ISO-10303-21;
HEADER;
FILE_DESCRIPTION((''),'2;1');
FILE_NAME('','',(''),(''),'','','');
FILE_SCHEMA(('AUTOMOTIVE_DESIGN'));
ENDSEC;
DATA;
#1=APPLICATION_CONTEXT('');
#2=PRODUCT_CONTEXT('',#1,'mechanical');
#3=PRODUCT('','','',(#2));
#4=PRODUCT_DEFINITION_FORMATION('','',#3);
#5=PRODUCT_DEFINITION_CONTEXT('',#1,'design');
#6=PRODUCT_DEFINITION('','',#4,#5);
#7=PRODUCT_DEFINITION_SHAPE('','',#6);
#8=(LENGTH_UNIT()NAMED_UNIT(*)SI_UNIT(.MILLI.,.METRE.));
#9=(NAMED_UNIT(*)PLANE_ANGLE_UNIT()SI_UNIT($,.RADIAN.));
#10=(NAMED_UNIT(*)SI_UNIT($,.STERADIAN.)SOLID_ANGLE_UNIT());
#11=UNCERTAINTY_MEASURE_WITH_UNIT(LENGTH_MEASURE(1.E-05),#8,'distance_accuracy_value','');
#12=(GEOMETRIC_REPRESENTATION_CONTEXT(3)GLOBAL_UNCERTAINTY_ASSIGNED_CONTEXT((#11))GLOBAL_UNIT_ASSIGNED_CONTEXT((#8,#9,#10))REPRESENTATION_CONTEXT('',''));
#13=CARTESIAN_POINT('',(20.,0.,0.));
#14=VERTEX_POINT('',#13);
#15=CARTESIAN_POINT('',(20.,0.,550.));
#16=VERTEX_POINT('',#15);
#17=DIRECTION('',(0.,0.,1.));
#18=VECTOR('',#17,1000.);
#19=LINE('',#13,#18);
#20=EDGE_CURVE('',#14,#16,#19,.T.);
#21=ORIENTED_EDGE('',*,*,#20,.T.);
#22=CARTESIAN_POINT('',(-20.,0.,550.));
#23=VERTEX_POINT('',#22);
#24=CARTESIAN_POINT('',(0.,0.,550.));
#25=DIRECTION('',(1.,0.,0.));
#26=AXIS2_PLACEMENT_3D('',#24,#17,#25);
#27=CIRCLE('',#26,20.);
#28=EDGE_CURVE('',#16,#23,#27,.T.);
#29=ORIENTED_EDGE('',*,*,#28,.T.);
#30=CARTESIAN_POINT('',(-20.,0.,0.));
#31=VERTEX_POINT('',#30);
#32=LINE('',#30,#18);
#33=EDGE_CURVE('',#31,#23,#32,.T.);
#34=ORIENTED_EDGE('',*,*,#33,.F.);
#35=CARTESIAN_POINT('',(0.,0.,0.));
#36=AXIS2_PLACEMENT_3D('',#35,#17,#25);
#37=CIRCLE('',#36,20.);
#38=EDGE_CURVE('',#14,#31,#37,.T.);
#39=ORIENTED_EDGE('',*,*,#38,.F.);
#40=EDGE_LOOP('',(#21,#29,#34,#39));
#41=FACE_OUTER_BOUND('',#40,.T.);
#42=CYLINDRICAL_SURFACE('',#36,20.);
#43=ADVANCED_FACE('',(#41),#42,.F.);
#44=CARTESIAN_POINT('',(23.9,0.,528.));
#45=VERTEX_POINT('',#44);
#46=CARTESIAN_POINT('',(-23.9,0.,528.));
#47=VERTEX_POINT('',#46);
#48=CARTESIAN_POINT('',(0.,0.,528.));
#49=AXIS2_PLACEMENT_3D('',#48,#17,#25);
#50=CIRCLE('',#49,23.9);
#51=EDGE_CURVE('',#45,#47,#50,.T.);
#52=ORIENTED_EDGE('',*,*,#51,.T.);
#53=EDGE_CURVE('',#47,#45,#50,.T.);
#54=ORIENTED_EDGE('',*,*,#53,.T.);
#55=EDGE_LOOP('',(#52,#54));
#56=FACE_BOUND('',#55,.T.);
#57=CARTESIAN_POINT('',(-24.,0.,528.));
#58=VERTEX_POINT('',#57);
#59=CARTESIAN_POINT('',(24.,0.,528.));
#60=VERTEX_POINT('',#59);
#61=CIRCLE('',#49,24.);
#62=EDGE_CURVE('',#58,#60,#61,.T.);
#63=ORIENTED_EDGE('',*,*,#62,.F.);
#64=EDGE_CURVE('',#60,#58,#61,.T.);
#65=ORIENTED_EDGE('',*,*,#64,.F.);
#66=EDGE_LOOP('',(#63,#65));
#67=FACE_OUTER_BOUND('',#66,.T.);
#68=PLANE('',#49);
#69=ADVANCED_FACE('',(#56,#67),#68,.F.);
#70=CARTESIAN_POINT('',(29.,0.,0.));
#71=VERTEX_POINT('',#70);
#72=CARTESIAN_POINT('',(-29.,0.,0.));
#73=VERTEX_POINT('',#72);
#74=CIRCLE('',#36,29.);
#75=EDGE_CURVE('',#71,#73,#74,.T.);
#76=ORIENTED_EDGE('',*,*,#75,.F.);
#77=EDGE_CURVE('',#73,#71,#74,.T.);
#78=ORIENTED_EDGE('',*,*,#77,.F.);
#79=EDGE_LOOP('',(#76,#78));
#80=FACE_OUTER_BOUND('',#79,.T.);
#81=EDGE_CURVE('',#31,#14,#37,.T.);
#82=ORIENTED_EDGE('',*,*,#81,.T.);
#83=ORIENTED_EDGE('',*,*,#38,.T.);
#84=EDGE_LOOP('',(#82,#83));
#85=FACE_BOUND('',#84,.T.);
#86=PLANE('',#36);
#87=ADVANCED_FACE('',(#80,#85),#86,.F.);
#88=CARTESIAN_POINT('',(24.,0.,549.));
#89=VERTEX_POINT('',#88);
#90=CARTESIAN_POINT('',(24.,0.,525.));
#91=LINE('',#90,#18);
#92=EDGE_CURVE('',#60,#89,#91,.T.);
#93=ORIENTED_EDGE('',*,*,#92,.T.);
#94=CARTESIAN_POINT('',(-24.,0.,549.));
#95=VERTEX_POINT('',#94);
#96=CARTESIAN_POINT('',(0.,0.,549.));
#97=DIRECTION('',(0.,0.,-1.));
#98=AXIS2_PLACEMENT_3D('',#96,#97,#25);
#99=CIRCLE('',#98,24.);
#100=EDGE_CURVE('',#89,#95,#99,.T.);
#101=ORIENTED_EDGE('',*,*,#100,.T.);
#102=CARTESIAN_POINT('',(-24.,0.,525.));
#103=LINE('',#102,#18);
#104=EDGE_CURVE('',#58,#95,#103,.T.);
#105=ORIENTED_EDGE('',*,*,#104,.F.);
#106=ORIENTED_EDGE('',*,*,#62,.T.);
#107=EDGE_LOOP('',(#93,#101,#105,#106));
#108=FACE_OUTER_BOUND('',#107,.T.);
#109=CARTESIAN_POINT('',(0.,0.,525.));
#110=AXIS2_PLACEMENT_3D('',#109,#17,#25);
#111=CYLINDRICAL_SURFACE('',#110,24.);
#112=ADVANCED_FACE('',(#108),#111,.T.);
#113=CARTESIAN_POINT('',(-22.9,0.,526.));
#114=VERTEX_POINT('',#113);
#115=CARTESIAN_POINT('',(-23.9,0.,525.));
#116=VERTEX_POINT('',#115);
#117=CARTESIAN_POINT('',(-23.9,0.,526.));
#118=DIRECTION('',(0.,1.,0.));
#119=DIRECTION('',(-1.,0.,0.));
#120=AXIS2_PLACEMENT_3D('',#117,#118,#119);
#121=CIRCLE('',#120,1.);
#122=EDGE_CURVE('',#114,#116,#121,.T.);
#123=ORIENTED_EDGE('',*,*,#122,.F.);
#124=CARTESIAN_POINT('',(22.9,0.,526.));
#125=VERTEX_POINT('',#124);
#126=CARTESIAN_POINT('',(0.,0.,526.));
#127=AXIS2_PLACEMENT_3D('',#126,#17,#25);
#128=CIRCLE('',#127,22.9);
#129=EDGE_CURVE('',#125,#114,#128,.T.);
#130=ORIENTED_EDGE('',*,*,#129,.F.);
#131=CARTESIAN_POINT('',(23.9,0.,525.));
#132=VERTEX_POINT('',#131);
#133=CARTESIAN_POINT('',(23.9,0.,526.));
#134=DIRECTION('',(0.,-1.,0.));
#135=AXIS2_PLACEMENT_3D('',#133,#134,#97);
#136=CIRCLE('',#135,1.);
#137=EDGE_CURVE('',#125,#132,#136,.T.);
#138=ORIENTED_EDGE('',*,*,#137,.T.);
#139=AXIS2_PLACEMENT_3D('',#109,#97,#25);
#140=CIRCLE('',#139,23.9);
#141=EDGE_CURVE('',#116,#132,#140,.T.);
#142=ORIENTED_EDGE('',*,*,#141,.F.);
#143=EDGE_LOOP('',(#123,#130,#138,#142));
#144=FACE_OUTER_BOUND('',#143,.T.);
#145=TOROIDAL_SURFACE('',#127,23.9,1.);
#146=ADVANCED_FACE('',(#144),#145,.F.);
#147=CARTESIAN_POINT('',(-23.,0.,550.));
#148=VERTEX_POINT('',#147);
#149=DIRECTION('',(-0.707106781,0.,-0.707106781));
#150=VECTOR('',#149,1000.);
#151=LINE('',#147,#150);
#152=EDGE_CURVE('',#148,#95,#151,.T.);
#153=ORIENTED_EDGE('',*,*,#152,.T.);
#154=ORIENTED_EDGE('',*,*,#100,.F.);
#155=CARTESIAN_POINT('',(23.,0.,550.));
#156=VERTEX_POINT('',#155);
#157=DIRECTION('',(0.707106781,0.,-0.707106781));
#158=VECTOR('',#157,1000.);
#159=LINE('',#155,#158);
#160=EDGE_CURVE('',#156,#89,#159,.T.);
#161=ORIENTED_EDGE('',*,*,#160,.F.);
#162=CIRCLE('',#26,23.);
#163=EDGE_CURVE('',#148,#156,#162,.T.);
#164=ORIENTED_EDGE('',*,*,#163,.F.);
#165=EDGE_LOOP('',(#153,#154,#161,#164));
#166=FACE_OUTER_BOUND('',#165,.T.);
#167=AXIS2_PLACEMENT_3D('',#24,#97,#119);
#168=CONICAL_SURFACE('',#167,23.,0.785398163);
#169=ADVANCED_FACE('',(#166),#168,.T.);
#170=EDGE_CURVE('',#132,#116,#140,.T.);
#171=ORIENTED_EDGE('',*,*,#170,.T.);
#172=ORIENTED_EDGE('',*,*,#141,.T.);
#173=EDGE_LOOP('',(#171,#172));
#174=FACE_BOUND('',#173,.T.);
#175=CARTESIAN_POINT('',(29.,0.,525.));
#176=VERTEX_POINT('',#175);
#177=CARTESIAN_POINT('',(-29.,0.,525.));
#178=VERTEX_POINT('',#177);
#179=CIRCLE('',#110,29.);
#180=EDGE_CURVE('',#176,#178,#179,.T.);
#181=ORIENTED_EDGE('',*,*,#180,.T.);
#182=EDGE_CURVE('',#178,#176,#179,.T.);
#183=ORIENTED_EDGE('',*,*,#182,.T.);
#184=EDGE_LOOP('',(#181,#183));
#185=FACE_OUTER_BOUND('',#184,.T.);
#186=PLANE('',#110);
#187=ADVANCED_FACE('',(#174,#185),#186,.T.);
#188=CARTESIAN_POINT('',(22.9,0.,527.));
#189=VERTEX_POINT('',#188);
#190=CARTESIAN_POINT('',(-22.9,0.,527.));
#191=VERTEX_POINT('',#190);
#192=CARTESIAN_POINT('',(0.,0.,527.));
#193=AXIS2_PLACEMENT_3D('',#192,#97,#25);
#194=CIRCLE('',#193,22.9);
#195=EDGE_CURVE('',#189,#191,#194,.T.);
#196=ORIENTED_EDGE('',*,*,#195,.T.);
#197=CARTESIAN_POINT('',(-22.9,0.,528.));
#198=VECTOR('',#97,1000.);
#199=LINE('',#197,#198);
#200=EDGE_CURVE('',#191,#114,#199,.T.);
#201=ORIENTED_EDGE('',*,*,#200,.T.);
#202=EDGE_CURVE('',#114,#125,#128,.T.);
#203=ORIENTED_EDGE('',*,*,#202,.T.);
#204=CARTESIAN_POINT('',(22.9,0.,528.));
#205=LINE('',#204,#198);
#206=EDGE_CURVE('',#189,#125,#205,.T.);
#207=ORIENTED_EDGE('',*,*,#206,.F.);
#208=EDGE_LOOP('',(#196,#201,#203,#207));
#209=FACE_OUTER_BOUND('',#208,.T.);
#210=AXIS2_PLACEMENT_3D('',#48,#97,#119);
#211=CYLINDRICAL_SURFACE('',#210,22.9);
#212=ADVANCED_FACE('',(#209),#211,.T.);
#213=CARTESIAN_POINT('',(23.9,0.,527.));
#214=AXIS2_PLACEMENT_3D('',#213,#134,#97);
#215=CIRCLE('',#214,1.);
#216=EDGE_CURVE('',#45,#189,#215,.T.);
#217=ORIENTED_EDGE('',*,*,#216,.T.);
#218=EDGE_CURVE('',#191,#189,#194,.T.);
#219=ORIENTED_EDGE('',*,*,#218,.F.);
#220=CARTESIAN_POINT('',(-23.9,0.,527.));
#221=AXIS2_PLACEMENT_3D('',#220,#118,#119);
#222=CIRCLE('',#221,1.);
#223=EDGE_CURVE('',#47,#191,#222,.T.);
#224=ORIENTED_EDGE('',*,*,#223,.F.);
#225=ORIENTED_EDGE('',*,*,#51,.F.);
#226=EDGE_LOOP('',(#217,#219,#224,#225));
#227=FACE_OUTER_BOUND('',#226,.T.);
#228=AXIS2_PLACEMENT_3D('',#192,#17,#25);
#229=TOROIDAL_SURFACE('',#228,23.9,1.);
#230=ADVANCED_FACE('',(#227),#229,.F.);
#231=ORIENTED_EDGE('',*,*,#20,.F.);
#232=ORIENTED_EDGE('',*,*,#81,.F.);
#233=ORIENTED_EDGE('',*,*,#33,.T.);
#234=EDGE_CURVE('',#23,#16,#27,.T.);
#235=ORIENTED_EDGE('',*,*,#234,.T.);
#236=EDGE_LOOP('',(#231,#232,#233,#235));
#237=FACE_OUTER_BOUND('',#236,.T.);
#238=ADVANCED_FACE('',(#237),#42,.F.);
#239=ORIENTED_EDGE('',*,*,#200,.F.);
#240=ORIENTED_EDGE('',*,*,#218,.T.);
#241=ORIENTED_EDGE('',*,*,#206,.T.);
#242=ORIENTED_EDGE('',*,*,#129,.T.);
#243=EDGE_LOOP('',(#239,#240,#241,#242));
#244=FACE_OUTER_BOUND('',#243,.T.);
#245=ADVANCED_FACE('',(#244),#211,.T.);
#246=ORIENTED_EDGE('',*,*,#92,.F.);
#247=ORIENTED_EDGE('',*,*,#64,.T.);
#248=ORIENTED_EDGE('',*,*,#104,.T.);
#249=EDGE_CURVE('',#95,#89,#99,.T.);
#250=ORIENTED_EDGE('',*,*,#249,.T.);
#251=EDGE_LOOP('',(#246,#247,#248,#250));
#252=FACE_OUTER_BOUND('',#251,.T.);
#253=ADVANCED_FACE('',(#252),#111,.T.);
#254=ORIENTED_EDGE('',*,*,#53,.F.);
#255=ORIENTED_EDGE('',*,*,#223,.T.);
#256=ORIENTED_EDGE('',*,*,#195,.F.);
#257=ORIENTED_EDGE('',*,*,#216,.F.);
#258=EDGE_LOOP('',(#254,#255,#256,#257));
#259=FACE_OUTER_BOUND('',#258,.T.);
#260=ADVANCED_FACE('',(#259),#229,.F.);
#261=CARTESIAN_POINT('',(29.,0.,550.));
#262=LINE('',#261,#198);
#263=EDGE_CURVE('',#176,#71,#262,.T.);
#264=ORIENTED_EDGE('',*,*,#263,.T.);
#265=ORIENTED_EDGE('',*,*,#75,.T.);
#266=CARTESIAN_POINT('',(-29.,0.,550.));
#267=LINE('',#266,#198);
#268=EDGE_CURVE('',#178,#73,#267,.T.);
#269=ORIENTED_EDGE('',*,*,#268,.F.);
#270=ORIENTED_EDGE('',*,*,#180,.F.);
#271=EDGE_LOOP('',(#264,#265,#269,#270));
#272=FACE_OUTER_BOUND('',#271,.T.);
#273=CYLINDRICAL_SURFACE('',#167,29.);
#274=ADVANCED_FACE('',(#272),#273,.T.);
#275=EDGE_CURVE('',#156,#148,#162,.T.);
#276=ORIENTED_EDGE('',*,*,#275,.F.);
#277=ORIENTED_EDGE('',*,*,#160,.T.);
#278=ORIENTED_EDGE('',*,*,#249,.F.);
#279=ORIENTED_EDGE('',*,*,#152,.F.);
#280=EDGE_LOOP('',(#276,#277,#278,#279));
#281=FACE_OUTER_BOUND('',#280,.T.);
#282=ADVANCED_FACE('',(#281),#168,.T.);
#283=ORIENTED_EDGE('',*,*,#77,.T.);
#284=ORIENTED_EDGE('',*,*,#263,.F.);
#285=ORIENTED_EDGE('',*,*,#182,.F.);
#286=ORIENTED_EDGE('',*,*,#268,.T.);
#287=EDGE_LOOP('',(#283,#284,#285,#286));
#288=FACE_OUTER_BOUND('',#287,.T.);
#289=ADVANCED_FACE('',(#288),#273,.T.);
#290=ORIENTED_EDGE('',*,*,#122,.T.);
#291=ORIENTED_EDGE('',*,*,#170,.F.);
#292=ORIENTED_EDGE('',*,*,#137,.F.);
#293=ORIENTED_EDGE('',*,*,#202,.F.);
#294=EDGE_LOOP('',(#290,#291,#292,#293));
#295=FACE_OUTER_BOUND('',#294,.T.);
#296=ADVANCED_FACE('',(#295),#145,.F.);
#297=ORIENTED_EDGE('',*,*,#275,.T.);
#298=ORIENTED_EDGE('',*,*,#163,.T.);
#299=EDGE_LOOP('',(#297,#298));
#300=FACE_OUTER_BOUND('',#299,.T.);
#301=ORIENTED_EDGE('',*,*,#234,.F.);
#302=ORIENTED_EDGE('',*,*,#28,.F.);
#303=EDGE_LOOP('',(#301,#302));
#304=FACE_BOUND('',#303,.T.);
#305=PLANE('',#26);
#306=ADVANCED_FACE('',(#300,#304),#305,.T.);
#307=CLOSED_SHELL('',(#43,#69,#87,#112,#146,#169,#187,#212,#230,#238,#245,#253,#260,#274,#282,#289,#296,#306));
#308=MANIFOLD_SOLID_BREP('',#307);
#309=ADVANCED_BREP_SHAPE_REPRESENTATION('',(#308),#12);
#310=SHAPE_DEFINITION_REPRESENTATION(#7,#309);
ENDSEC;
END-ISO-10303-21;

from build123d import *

# Parameters (mm, degrees)
SKETCH1_R           = 29
BOSS_EXTRUDE1_DEPTH = 550
CUT_EXTRUDE1_START  = -25
SKETCH2_R           = 29
SKETCH2_R_2         = 24
CUT_EXTRUDE1_DEPTH  = 25
SKETCH3_R           = 20
CUT_EXTRUDE2_DEPTH  = 552.526971235
CHAMFER1_SIZE       = 1
SKETCH4_R           = 24
SKETCH4_R_2         = 22.9
CUT_EXTRUDE3_DEPTH  = 3
FILLET1_R           = 1


with BuildPart() as part:
    # Sketch1 → Boss-Extrude1 (new body)
    with BuildSketch(Plane.XY):
        Circle(SKETCH1_R)
    extrude(amount=BOSS_EXTRUDE1_DEPTH)

    # Sketch2 → Cut-Extrude1 (cut)
    with BuildSketch(Plane.XY.offset(550).offset(CUT_EXTRUDE1_START)):
        Circle(SKETCH2_R)
        Circle(SKETCH2_R_2, mode=Mode.SUBTRACT)
    extrude(amount=CUT_EXTRUDE1_DEPTH, mode=Mode.SUBTRACT)

    # Sketch3 → Cut-Extrude2 (cut, through all)
    with BuildSketch(Plane.XY.offset(550)):
        Circle(SKETCH3_R)
    extrude(amount=-CUT_EXTRUDE2_DEPTH, mode=Mode.SUBTRACT)

    # Chamfer1
    chamfer1_edges = [part.edges().sort_by_distance(p)[0] for p in [
        (-24, 0, 550),
    ]]
    chamfer(chamfer1_edges, length=CHAMFER1_SIZE)

    # Sketch4 → Cut-Extrude3 (cut)
    with BuildSketch(Plane.XY.offset(525)):
        Circle(SKETCH4_R)
        Circle(SKETCH4_R_2, mode=Mode.SUBTRACT)
    extrude(amount=CUT_EXTRUDE3_DEPTH, mode=Mode.SUBTRACT)

    # Fillet1
    fillet1_edges = [part.edges().sort_by_distance(p)[0] for p in [
        (-22.9, 0, 525),
        (-22.9, 0, 528),
    ]]
    fillet(fillet1_edges, radius=FILLET1_R)


solid = part.part
